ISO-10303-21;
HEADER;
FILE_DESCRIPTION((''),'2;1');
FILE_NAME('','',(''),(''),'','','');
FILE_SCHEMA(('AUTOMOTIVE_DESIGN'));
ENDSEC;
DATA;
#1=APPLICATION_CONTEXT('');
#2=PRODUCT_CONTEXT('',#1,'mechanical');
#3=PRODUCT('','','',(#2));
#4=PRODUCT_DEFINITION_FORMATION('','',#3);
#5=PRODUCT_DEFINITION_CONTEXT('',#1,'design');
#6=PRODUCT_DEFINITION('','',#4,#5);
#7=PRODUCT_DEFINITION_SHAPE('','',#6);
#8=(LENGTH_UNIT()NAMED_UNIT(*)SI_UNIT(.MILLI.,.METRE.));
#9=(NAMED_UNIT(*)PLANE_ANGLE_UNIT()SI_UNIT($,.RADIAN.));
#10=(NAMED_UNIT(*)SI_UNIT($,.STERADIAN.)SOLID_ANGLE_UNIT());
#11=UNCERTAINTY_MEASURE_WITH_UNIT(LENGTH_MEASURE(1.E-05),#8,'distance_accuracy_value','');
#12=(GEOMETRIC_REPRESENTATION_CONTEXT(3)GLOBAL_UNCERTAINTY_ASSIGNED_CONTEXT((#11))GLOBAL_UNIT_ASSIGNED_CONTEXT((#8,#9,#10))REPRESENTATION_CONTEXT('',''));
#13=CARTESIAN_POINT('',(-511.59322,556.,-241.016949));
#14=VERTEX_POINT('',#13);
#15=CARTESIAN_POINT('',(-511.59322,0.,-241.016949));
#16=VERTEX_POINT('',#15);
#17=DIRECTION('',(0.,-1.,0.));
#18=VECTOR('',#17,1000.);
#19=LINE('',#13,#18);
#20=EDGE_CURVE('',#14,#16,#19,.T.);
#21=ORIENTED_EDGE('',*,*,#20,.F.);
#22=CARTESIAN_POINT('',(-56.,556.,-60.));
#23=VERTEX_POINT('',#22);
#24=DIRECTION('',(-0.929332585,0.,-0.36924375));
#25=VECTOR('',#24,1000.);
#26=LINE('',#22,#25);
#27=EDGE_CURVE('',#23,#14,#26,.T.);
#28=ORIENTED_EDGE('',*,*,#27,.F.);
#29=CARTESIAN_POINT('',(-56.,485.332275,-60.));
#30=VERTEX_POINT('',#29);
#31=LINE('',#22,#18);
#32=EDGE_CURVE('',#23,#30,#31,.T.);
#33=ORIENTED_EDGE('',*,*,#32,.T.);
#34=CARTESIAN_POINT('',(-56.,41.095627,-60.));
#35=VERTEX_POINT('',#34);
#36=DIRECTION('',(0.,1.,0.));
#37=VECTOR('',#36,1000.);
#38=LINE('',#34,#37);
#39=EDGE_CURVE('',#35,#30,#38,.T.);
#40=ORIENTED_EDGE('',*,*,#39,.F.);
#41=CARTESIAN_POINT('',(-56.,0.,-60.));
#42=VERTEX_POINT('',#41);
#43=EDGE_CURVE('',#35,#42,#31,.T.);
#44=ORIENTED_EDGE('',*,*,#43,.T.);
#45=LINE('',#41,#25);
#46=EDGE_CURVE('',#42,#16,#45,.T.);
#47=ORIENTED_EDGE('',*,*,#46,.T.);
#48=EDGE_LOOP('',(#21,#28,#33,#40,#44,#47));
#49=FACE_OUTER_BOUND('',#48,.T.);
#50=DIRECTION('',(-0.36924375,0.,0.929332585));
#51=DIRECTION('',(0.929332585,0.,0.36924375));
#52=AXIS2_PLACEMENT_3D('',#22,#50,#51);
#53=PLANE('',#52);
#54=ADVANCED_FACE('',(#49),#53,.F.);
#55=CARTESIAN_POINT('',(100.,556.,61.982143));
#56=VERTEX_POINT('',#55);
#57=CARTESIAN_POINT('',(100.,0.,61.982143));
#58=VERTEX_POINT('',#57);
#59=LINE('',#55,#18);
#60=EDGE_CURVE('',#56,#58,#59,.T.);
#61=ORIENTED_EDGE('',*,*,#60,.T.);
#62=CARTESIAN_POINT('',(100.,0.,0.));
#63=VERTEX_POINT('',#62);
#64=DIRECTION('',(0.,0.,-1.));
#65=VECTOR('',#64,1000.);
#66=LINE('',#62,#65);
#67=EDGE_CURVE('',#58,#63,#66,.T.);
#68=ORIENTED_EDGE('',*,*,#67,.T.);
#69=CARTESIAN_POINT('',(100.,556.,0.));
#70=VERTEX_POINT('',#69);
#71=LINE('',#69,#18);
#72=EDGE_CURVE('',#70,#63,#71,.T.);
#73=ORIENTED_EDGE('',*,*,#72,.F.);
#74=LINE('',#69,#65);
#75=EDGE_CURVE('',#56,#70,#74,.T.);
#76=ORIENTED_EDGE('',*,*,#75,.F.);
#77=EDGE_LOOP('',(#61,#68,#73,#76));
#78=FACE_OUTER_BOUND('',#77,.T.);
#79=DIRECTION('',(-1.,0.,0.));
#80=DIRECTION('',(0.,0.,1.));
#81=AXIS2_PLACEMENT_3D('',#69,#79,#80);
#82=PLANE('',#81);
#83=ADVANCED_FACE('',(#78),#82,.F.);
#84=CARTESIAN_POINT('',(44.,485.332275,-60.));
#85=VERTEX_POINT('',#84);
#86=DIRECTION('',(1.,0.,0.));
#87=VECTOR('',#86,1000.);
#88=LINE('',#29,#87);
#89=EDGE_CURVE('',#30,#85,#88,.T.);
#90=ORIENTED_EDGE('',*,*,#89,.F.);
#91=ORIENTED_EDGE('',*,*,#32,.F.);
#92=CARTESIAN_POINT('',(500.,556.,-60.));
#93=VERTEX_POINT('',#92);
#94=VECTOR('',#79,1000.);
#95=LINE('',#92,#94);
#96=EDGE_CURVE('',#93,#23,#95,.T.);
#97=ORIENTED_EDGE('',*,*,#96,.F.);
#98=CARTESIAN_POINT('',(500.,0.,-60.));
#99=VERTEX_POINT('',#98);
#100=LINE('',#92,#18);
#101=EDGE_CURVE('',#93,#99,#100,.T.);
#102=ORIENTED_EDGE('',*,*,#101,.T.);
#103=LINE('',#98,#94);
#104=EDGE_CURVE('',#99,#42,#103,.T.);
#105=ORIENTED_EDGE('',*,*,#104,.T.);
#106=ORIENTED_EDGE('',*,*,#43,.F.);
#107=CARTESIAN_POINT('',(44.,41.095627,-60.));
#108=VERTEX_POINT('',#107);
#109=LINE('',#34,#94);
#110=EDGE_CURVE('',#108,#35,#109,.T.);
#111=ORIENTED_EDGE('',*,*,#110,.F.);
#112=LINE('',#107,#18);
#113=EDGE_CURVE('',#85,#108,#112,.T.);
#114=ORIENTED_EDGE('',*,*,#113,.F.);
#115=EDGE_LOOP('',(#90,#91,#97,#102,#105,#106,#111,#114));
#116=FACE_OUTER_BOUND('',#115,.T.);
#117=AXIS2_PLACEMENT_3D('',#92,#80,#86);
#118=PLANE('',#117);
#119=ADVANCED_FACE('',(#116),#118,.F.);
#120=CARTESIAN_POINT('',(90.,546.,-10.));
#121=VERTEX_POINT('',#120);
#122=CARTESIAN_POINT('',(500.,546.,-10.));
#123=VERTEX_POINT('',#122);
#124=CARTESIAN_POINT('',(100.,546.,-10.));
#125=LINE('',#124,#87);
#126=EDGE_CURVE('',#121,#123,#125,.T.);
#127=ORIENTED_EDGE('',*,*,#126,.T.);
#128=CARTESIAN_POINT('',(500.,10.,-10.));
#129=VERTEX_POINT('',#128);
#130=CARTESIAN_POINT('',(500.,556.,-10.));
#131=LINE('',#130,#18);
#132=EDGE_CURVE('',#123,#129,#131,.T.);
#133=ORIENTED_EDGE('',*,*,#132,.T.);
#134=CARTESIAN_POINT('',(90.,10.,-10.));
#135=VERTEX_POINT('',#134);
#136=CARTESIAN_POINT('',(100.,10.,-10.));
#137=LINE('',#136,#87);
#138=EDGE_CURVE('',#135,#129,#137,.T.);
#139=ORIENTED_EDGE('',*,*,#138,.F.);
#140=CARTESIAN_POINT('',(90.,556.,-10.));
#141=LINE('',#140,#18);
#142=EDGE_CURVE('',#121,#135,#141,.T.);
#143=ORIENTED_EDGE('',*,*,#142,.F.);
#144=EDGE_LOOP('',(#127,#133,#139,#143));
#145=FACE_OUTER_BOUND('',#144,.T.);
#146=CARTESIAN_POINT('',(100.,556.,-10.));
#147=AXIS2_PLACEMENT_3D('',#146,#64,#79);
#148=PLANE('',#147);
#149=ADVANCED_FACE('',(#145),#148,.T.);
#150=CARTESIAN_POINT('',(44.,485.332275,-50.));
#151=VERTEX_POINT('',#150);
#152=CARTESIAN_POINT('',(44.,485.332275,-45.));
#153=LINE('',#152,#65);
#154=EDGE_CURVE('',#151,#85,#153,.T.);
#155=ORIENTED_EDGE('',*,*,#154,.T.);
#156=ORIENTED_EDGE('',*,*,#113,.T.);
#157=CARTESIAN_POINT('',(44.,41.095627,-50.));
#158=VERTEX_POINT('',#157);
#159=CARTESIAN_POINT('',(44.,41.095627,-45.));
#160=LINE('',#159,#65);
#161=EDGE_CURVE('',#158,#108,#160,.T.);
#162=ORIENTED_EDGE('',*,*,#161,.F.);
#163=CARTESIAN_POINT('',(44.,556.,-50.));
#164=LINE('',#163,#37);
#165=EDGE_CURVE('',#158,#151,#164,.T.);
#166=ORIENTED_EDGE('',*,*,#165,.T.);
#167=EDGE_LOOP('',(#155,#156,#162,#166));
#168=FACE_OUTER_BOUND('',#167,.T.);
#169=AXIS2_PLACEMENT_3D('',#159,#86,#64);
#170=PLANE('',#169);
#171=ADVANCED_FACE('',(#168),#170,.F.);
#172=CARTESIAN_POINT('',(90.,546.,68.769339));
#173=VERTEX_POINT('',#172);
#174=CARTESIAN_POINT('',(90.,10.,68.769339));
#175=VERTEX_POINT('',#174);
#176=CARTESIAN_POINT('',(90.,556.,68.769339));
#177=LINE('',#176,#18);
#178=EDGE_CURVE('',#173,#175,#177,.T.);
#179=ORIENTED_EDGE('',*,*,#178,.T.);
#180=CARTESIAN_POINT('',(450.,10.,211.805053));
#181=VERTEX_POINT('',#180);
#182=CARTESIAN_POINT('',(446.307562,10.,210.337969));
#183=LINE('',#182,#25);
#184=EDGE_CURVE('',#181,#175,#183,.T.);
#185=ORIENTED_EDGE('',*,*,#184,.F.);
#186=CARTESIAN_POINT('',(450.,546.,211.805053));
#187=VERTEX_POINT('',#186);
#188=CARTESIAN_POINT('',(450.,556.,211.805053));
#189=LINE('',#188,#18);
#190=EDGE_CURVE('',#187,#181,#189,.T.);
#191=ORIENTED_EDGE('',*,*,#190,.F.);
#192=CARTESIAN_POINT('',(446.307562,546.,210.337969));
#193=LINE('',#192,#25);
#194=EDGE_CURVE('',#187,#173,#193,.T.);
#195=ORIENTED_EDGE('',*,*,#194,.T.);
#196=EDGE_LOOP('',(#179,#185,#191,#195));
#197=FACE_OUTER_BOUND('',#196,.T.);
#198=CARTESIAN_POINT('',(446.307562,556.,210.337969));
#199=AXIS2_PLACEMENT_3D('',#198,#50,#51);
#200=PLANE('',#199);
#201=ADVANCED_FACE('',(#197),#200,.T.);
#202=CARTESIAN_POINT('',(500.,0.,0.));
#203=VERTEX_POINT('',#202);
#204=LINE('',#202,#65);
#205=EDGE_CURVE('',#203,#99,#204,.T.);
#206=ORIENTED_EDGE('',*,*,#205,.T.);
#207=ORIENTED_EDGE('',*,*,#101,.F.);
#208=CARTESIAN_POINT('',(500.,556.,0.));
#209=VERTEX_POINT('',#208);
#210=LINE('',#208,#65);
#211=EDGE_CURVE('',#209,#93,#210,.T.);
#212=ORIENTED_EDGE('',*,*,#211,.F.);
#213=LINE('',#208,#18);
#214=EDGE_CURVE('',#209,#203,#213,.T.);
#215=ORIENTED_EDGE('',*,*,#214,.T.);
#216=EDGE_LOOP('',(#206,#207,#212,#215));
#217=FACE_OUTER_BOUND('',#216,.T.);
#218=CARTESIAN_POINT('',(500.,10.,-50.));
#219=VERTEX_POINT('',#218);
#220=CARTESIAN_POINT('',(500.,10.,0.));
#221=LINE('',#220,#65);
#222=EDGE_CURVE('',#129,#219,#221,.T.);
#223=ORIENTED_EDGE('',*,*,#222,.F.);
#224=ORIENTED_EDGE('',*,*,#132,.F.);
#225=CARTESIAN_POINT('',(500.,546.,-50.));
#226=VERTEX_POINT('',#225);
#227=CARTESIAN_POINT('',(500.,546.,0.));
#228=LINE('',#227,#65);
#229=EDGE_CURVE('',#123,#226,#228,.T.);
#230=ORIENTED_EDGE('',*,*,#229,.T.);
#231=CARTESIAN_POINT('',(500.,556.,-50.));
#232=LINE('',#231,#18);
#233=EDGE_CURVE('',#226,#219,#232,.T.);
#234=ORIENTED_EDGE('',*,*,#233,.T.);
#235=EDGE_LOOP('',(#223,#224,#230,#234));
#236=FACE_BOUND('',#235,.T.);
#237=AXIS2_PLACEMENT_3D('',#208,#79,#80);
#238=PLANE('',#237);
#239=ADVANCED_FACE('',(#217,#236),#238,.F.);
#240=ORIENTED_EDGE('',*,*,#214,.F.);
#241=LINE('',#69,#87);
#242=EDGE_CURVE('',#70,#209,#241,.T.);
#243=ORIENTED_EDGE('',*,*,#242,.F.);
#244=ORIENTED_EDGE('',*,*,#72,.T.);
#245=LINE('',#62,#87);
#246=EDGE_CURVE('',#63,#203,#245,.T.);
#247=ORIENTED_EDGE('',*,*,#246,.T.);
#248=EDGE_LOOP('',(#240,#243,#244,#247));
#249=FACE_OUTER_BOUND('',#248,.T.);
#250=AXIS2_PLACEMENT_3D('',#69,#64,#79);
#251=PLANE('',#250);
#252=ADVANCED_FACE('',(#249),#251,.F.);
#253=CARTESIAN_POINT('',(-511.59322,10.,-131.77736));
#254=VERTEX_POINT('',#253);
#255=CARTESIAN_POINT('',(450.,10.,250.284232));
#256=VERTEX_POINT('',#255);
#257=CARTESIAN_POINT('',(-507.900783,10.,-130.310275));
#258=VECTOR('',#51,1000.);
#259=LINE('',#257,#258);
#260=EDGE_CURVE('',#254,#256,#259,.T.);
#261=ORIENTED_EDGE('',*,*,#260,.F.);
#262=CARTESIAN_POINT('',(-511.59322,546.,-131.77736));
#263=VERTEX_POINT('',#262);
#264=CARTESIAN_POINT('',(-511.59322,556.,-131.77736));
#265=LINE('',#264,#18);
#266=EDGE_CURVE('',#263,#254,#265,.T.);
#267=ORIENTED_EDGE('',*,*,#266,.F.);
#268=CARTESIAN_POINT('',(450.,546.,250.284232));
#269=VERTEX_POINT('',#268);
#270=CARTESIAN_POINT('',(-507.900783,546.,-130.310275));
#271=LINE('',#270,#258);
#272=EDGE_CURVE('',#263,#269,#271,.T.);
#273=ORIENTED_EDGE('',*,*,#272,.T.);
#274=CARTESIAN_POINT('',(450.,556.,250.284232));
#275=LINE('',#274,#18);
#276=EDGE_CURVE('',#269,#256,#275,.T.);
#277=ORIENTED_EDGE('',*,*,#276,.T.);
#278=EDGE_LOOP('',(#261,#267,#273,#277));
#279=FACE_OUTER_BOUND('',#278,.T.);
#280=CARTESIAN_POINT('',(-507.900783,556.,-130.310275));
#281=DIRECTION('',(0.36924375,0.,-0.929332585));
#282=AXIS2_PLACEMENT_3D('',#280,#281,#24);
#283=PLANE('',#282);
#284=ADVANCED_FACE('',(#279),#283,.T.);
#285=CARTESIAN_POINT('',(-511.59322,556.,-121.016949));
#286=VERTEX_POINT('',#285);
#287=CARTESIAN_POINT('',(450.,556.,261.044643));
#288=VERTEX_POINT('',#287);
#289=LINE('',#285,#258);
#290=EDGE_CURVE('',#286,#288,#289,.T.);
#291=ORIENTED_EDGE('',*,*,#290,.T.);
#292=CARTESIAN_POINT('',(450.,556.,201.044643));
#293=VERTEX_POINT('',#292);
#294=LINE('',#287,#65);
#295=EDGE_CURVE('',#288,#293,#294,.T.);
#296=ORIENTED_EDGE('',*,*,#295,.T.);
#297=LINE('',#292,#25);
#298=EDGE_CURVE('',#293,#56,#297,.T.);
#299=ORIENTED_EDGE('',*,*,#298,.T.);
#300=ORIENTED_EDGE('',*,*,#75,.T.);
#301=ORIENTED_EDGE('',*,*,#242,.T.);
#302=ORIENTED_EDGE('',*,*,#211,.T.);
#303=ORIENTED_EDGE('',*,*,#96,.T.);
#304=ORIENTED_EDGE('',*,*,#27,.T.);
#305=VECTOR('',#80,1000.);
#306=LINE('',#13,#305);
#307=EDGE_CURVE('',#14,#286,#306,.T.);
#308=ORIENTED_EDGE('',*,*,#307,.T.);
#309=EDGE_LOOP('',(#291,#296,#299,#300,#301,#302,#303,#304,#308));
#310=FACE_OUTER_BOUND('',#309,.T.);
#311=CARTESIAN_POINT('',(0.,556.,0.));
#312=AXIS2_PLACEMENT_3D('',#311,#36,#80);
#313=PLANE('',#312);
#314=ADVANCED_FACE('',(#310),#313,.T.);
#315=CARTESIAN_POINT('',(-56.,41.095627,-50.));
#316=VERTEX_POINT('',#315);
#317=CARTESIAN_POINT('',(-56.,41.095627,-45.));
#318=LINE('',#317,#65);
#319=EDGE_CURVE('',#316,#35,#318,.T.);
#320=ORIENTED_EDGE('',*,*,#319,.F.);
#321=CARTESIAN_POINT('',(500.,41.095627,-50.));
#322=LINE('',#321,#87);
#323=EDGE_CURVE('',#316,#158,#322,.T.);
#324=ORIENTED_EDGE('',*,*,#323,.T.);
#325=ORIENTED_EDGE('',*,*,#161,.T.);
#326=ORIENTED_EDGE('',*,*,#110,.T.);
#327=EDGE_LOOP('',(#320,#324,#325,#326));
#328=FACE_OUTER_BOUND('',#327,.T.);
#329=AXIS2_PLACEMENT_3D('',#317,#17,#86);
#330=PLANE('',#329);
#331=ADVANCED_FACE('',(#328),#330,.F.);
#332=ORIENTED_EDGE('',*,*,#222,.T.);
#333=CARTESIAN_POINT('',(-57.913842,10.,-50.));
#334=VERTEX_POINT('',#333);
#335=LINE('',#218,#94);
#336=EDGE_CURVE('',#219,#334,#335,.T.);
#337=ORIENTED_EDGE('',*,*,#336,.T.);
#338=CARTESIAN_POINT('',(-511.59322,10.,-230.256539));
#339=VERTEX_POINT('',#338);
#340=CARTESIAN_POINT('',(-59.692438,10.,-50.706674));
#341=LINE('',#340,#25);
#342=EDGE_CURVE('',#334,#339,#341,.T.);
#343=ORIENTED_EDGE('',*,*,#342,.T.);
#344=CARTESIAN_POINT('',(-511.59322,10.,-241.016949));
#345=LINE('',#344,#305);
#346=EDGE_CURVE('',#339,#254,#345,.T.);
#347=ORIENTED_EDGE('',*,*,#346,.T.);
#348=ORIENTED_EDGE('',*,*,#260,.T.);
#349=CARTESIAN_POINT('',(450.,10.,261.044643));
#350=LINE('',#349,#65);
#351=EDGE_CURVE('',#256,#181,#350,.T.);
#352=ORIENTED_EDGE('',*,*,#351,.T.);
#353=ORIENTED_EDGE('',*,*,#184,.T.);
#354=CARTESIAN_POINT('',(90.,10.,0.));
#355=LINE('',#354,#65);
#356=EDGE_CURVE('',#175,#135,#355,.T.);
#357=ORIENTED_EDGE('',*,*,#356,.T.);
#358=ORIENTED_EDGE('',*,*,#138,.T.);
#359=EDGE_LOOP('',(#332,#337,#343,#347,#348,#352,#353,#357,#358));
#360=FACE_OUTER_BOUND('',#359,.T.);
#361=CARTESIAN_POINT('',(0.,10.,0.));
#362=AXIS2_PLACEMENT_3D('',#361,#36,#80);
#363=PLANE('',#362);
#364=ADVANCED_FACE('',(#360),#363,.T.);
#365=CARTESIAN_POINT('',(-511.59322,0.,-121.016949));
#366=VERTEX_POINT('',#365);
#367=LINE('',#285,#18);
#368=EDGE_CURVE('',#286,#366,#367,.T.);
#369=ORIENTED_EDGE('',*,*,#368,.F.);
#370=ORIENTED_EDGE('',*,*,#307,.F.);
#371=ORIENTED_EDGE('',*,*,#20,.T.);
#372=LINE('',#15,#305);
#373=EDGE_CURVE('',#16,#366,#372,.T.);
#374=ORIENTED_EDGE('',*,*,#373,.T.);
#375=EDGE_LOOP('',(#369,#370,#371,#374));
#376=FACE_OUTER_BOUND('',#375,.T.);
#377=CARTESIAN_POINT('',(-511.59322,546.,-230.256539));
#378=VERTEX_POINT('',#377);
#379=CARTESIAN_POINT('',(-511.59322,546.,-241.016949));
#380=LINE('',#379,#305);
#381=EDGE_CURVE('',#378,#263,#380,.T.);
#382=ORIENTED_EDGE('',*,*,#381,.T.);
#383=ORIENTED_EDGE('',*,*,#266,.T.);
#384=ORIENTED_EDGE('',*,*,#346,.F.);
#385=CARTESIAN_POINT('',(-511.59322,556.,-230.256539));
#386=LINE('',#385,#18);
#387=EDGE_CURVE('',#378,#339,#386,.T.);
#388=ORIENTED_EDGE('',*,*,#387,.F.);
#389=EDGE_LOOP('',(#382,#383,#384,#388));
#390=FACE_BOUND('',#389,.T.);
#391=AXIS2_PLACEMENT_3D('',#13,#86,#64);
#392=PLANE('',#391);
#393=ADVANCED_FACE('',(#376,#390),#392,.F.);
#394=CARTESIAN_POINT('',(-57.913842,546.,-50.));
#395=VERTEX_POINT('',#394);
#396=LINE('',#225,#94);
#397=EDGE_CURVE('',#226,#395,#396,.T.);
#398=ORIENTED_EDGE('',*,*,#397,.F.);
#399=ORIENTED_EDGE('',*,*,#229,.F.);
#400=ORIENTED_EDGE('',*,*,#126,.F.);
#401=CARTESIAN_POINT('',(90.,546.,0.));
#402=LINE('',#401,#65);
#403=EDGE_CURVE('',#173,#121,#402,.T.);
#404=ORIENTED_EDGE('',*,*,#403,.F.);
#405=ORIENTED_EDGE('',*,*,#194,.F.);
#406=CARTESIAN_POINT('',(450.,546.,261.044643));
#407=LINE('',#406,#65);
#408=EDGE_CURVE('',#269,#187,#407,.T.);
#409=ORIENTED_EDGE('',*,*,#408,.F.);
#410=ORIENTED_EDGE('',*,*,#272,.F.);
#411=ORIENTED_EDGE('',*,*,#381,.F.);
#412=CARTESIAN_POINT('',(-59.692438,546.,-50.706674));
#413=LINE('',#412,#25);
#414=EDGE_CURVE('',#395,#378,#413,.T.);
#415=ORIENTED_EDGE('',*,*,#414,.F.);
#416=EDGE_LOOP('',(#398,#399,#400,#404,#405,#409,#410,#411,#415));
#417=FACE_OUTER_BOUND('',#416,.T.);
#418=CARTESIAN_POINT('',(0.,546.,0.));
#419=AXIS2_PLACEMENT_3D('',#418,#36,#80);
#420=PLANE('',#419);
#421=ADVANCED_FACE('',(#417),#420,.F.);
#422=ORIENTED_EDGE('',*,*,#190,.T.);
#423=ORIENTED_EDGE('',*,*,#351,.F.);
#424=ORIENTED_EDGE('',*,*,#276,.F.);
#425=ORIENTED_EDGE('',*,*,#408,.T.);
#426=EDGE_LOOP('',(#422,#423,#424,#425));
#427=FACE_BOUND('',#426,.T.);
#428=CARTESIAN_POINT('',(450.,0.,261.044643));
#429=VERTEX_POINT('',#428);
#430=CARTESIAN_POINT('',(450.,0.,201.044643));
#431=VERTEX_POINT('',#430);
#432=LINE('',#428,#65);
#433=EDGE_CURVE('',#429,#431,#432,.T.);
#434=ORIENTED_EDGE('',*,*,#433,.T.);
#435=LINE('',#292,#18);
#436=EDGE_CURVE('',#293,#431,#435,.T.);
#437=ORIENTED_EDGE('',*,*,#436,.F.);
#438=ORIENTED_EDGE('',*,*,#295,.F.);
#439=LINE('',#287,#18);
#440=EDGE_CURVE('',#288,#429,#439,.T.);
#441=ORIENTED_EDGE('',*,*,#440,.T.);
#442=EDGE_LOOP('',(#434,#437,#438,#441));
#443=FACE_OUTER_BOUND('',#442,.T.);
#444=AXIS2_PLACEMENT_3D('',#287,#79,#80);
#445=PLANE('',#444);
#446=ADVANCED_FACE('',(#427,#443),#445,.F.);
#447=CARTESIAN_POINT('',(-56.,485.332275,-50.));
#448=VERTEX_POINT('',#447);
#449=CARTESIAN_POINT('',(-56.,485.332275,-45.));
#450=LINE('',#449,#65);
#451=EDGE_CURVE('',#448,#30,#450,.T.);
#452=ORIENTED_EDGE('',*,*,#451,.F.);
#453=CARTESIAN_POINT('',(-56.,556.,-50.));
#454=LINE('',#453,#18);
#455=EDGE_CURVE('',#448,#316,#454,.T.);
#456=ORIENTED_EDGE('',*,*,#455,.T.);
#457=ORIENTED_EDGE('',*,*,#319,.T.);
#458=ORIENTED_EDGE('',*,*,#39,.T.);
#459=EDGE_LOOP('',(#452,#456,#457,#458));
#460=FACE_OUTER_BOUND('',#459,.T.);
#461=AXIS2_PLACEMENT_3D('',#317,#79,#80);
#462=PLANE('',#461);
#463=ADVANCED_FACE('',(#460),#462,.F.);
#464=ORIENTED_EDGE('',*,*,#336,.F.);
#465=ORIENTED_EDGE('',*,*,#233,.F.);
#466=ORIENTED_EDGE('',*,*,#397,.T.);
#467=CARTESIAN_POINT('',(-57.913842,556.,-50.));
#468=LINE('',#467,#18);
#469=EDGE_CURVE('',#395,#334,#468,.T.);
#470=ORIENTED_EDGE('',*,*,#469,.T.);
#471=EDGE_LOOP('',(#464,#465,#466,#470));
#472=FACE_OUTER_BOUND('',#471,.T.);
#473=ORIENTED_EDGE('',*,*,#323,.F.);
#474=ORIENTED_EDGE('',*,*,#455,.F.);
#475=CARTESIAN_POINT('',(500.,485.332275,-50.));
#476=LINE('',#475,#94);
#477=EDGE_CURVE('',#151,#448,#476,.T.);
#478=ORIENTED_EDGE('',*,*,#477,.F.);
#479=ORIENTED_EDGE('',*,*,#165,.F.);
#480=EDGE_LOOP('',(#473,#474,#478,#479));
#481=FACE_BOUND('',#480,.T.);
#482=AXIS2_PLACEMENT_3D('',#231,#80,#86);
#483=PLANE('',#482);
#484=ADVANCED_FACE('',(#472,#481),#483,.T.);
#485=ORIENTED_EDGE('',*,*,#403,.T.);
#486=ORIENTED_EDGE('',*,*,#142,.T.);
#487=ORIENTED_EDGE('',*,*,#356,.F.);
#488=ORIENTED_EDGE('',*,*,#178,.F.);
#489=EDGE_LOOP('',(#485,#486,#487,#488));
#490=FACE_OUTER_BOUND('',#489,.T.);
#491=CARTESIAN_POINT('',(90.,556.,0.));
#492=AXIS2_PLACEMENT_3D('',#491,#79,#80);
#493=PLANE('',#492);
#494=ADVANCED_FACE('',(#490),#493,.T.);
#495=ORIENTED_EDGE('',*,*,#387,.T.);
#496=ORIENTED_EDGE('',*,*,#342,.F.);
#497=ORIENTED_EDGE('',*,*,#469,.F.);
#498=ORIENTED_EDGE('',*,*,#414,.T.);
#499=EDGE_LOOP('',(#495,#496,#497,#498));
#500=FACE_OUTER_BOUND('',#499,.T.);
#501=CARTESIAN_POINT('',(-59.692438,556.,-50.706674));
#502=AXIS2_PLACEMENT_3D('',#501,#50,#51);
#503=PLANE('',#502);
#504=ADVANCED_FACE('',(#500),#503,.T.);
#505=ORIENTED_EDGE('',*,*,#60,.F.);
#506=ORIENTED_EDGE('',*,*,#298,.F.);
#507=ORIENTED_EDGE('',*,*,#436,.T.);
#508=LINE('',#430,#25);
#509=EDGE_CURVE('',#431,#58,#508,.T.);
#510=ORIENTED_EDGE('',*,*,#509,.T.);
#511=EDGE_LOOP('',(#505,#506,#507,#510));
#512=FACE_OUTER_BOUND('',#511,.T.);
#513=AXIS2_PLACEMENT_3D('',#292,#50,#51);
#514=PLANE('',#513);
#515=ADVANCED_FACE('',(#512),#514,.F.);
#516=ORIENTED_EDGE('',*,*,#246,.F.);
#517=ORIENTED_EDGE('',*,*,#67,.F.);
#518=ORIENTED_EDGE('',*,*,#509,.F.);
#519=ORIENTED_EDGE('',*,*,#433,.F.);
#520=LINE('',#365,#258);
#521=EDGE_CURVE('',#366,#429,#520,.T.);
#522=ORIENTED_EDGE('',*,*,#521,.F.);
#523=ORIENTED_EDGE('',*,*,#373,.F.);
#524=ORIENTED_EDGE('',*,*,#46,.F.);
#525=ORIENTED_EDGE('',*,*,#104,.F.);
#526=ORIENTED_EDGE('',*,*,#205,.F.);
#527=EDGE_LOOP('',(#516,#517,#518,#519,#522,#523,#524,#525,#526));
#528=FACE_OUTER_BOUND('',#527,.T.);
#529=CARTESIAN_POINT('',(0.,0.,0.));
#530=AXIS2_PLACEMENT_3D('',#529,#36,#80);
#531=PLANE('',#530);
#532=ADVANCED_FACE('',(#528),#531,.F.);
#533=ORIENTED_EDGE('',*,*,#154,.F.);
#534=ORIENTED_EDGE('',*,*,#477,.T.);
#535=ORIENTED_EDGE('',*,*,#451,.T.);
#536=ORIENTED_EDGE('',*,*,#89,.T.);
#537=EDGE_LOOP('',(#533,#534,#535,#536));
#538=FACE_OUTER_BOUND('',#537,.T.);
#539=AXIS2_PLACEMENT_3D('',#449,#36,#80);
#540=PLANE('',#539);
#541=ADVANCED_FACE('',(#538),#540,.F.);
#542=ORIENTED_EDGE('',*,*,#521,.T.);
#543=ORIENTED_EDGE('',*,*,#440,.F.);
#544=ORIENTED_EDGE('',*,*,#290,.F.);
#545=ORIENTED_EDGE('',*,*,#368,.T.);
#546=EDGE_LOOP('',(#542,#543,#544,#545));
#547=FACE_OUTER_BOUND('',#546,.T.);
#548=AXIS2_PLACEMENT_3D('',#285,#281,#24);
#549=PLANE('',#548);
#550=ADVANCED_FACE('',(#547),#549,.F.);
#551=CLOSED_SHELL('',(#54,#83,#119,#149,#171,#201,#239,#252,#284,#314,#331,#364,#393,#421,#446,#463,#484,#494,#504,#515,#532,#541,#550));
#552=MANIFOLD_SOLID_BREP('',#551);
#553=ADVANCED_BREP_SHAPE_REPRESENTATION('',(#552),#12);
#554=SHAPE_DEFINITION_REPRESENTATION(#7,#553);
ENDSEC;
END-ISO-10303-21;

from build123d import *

# Parameters (mm, degrees)
BOSS_EXTRUDE1_DEPTH = 556
SHELL1_T            = -10
SKETCH2_W           = 100
SKETCH2_H           = 444.236647894
CUT_EXTRUDE1_DEPTH  = 15


with BuildPart() as part:
    # Sketch1 → Boss-Extrude1 (new body)
    with BuildSketch(Plane(origin=(0, 0, 0), x_dir=(1, 0, 0), z_dir=(0, 1, 0))):
        Polygon((100, 0), (500, 0), (500, 60), (-56, 60), (-511.593220339, 241.016949153), (-511.593220339, 121.016949153), (450, -261.044642857), (450, -201.044642857), (100, -61.982142857), align=None)
    extrude(amount=BOSS_EXTRUDE1_DEPTH)

    # Shell1
    shell1_openings = [part.faces().sort_by_distance(p)[0] for p in [
        (450, 278, 231.044642857),
        (-511.593220339, 278, -181.016949153),
        (500, 278, -30),
    ]]
    offset(amount=SHELL1_T, openings=shell1_openings, kind=Kind.INTERSECTION)

    # Sketch2 → Cut-Extrude1 (cut)
    with BuildSketch(Plane(origin=(0, 0, -60), x_dir=(-1, 0, 0), z_dir=(0, 0, -1))):
        with Locations((6, 263.213951143)):
            Rectangle(SKETCH2_W, SKETCH2_H)
    extrude(amount=-CUT_EXTRUDE1_DEPTH, mode=Mode.SUBTRACT)


solid = part.part
